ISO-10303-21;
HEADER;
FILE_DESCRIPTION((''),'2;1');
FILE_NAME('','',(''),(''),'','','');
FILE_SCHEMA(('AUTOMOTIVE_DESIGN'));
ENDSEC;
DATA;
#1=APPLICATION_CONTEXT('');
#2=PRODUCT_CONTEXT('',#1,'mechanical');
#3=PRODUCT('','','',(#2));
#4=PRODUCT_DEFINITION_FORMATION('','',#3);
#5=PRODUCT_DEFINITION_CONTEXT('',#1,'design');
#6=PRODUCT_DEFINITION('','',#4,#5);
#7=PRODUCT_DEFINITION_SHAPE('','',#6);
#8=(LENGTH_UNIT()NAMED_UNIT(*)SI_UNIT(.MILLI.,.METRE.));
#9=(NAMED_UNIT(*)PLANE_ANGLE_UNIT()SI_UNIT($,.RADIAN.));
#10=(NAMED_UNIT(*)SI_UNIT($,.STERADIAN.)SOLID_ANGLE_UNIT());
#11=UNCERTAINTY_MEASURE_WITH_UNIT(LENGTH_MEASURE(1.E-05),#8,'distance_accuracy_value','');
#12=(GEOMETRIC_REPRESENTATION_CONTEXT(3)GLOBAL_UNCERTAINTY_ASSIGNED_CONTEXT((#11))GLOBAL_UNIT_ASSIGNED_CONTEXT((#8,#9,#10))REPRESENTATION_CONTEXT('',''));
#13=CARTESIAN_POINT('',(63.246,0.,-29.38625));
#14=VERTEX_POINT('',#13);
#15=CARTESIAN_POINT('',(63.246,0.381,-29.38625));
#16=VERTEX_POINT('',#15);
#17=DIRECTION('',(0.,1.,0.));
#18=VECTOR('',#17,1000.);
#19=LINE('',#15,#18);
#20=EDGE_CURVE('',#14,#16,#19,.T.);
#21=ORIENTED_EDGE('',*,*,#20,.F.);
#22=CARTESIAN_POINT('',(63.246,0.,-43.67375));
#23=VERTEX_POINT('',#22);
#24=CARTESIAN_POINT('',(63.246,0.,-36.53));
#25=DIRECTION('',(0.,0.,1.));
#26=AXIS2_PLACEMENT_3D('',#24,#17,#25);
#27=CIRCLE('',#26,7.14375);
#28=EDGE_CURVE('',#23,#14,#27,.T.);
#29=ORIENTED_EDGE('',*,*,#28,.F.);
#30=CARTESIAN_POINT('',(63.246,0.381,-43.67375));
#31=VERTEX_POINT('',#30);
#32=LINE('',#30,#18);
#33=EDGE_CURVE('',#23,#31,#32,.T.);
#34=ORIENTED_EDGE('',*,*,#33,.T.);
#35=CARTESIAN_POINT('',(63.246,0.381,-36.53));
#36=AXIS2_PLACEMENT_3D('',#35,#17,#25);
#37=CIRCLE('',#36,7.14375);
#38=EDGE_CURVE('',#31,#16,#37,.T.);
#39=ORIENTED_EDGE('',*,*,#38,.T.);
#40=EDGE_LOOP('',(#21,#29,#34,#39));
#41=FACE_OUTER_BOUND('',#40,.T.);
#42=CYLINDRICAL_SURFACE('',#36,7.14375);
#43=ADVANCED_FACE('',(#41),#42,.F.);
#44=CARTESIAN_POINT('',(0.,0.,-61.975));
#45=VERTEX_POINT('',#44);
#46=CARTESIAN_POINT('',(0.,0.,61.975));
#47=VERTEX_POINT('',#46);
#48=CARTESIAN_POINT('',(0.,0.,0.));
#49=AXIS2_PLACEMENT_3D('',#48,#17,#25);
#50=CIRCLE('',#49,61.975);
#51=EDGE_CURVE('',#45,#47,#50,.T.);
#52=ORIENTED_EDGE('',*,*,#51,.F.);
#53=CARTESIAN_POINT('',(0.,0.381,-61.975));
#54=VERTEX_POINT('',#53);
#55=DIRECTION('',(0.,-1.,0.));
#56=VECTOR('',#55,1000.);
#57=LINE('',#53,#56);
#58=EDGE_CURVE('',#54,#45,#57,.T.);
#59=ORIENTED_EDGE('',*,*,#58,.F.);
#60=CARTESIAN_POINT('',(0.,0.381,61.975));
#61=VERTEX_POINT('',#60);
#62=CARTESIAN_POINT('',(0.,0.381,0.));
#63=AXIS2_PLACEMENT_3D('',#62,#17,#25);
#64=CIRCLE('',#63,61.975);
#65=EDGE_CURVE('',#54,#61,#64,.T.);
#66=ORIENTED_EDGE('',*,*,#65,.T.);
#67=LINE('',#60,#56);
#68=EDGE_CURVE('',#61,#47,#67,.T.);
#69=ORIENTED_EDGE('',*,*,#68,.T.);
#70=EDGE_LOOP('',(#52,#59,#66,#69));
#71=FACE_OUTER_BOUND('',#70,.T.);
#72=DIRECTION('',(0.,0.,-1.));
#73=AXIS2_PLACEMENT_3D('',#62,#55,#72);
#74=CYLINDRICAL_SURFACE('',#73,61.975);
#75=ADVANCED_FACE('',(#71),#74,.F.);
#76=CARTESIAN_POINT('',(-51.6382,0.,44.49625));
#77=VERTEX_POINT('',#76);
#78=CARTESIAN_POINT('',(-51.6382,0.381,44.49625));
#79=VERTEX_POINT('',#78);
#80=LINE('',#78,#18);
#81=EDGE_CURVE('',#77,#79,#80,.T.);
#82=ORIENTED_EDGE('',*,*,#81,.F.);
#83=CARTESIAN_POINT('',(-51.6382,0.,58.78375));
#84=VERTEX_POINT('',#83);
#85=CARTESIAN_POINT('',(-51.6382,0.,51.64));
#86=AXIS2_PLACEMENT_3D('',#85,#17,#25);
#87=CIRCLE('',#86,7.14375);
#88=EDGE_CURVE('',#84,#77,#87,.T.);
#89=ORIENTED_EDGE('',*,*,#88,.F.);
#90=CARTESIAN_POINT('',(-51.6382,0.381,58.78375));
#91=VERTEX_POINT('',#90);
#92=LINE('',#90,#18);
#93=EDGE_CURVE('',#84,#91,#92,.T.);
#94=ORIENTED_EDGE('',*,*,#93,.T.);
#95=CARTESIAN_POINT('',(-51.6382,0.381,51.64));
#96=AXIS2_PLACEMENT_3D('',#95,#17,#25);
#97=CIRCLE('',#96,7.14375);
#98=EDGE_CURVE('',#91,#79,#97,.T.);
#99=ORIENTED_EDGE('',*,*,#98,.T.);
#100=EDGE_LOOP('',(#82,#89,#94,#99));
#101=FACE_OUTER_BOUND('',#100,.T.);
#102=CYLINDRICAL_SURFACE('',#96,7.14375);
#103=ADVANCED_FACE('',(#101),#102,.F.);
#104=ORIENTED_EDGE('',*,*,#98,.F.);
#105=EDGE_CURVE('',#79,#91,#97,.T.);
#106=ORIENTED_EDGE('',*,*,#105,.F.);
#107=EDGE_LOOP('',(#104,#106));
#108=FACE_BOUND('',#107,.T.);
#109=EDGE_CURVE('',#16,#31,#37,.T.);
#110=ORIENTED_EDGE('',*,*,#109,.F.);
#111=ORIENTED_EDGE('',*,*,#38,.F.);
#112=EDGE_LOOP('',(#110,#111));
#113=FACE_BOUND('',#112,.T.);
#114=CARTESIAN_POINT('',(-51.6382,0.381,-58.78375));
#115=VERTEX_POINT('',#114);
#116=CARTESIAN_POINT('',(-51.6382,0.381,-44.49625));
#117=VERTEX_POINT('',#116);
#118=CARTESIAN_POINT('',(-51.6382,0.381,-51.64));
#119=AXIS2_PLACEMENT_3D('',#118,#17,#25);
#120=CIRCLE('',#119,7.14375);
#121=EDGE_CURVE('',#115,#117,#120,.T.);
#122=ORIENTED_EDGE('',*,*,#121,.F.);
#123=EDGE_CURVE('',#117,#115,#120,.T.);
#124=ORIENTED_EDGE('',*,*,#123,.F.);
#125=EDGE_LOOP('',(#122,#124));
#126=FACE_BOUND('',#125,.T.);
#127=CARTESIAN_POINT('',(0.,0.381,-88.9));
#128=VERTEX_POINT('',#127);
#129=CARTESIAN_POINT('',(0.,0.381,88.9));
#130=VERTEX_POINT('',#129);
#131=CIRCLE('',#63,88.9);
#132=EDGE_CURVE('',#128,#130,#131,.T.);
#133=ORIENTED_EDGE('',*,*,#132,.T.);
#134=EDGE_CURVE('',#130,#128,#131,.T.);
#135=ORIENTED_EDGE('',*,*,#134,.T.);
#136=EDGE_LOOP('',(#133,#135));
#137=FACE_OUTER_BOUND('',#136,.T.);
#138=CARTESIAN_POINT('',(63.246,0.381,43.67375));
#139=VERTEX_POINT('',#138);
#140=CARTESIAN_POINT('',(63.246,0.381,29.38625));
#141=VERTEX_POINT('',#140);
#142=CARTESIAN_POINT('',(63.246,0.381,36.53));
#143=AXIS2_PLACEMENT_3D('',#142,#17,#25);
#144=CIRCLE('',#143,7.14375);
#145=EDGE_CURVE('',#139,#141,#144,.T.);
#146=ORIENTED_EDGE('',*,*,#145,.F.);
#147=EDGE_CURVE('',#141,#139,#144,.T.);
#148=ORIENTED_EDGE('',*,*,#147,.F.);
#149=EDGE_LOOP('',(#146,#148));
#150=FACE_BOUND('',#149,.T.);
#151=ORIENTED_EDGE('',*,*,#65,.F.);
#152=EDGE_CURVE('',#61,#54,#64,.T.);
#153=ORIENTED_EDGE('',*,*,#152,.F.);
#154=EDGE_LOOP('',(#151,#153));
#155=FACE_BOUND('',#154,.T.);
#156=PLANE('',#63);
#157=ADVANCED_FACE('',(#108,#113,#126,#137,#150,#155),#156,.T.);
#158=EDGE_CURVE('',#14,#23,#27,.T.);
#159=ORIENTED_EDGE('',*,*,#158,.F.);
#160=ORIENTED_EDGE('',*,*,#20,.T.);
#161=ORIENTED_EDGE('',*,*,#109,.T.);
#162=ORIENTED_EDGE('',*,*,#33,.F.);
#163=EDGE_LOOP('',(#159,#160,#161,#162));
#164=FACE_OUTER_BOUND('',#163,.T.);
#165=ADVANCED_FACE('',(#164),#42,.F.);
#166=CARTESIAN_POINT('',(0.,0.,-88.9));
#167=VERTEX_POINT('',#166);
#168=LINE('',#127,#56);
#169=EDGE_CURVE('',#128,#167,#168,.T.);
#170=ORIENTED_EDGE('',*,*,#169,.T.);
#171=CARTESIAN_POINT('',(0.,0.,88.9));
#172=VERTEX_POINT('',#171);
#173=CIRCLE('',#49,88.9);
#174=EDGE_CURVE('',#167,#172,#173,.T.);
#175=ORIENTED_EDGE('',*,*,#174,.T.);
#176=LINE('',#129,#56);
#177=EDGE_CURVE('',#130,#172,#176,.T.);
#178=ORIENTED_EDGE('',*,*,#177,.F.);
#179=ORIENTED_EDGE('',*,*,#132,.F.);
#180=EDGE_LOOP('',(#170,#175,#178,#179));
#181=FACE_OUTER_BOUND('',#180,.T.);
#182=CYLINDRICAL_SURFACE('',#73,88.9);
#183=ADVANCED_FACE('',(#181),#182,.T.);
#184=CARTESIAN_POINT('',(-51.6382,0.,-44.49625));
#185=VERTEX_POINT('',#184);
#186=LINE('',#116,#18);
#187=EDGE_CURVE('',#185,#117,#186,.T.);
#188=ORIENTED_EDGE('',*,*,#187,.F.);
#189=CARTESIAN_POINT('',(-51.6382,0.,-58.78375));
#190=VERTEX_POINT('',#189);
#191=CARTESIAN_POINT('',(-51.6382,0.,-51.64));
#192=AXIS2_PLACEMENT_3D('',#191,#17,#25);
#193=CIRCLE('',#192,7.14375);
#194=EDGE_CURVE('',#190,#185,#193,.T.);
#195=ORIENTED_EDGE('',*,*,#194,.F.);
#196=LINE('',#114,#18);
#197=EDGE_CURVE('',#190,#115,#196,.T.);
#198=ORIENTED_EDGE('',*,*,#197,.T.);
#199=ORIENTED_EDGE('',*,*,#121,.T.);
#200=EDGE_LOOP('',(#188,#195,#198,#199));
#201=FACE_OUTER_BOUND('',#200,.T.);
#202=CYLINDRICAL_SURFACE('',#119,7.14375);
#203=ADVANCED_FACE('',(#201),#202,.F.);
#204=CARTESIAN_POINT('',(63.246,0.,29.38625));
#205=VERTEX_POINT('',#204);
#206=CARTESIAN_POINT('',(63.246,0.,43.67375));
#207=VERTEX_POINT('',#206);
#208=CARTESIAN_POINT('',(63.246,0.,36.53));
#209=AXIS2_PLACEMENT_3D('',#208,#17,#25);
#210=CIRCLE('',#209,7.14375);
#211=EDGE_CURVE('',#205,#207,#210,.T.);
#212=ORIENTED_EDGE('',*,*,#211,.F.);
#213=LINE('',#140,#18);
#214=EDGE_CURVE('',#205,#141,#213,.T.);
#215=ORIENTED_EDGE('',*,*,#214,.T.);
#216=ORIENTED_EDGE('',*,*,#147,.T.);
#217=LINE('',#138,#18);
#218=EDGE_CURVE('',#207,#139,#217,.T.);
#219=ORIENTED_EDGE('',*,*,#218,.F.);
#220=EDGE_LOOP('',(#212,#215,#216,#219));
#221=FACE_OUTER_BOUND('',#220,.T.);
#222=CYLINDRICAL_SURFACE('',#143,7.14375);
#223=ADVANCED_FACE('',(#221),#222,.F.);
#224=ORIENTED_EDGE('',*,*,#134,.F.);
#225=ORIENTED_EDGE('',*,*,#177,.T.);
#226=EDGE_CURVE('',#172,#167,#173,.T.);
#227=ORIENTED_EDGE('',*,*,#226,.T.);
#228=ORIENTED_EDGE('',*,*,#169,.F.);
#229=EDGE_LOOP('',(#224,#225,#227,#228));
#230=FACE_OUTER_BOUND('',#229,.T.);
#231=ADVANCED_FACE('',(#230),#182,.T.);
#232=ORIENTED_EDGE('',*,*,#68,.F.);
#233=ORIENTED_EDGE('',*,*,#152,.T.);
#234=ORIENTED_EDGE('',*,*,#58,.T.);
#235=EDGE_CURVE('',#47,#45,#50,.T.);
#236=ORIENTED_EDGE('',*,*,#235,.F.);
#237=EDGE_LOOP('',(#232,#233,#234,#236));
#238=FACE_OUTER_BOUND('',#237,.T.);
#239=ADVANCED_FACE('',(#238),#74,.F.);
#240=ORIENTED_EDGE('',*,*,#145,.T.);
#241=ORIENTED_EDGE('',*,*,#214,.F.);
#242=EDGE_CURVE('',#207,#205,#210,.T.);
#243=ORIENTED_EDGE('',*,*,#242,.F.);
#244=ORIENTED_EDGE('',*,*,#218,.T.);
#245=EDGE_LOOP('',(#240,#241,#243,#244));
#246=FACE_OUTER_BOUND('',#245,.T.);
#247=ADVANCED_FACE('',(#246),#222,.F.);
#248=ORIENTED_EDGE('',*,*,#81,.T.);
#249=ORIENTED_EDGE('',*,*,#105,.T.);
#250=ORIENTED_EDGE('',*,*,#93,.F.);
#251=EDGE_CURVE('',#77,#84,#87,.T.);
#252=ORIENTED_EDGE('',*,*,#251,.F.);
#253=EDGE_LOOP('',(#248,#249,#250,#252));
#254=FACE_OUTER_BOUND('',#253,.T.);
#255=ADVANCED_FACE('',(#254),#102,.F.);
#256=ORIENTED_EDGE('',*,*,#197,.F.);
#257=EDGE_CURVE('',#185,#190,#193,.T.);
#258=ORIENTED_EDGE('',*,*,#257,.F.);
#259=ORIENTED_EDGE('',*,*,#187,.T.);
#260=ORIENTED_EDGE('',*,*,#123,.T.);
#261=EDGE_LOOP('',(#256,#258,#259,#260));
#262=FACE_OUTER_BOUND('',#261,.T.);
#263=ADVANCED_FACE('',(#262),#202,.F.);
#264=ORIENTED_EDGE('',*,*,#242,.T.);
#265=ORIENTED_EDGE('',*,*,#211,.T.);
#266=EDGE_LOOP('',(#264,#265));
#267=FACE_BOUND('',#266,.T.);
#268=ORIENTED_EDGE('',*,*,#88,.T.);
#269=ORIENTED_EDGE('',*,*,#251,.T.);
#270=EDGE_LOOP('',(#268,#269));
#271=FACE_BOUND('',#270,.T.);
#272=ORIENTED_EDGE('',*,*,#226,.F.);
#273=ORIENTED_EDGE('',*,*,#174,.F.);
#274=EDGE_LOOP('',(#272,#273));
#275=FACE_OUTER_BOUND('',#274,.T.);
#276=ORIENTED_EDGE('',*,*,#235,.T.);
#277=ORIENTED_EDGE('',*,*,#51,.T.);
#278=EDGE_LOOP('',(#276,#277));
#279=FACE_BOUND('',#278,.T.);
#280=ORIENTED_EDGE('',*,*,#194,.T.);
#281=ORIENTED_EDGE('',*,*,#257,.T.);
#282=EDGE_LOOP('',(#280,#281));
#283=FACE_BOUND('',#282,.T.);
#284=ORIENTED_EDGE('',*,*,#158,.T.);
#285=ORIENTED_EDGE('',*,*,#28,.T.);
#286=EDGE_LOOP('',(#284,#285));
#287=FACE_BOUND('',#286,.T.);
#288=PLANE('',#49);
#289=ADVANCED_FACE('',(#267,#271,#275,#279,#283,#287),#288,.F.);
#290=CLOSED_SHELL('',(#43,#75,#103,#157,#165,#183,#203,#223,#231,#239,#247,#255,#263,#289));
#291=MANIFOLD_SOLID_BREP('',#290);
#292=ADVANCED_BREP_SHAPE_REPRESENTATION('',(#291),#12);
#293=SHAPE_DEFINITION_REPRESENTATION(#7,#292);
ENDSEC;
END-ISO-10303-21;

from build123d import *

# Parameters (mm, degrees)
SKETCH1_R                               = 88.9
SKETCH1_R_2                             = 61.975
BOSS_EXTRUDE1_DEPTH                     = 0.381
F_9_16_0_5625_DIAMETER_HOLE1_AT_2_COUNT = 2
F_9_16_0_5625_DIAMETER_HOLE1_AT_2_PITCH = 144.818259586


with BuildPart() as part:
    # Sketch1 → Boss-Extrude1 (new body)
    with BuildSketch(Plane(origin=(0, 0, 0), x_dir=(1, 0, 0), z_dir=(0, 1, 0))):
        with Locations(Location((0, 0, 0), (0, 0, 90))):
            Circle(SKETCH1_R)
        with Locations(Location((0, 0, 0), (0, 0, 90))):
            Circle(SKETCH1_R_2, mode=Mode.SUBTRACT)
    extrude(amount=BOSS_EXTRUDE1_DEPTH)

    # Sketch2 → 9/16 (0.5625) Diameter Hole1 (revolve, cut)
    with BuildSketch(Plane(origin=(-51.6382, 0.381, -51.64), x_dir=(0, 0, 1), z_dir=(1, 0, 0))):
        Polygon((0, 0), (0, 20.172398047), (7.14375, 15.88), (7.14375, 0), align=None)
    f_9_16_0_5625_diameter_hole1 = revolve(axis=Axis((-51.6382, 6.731, -51.64), (0, -1, 0)), mode=Mode.SUBTRACT)

    # 9/16 (0.5625) Diameter Hole1 at 2: 9/16 (0.5625) Diameter Hole1 ×2
    with Locations(*[Vector(0.7932991345710956, 0, 0.6088320647672483) * (i * F_9_16_0_5625_DIAMETER_HOLE1_AT_2_PITCH) for i in range(1, F_9_16_0_5625_DIAMETER_HOLE1_AT_2_COUNT)]):
        add(f_9_16_0_5625_diameter_hole1, mode=Mode.SUBTRACT)

    # Mirror1: 9/16 (0.5625) Diameter Hole1 across plane
    add(f_9_16_0_5625_diameter_hole1.mirror(Plane.XY), mode=Mode.SUBTRACT)

    # Mirror1 copy 1 sketch → Mirror1 copy 1 (revolve, cut)
    with BuildSketch(Plane(origin=(63.246, 0.381, -36.53), x_dir=(0, 0, -1), z_dir=(1, 0, 0))):
        Polygon((0, 0), (0, -20.172398047), (7.14375, -15.88), (7.14375, 0), align=None)
    revolve(axis=Axis((63.246, 6.731, -36.53), (0, 1, 0)), mode=Mode.SUBTRACT)


solid = part.part
